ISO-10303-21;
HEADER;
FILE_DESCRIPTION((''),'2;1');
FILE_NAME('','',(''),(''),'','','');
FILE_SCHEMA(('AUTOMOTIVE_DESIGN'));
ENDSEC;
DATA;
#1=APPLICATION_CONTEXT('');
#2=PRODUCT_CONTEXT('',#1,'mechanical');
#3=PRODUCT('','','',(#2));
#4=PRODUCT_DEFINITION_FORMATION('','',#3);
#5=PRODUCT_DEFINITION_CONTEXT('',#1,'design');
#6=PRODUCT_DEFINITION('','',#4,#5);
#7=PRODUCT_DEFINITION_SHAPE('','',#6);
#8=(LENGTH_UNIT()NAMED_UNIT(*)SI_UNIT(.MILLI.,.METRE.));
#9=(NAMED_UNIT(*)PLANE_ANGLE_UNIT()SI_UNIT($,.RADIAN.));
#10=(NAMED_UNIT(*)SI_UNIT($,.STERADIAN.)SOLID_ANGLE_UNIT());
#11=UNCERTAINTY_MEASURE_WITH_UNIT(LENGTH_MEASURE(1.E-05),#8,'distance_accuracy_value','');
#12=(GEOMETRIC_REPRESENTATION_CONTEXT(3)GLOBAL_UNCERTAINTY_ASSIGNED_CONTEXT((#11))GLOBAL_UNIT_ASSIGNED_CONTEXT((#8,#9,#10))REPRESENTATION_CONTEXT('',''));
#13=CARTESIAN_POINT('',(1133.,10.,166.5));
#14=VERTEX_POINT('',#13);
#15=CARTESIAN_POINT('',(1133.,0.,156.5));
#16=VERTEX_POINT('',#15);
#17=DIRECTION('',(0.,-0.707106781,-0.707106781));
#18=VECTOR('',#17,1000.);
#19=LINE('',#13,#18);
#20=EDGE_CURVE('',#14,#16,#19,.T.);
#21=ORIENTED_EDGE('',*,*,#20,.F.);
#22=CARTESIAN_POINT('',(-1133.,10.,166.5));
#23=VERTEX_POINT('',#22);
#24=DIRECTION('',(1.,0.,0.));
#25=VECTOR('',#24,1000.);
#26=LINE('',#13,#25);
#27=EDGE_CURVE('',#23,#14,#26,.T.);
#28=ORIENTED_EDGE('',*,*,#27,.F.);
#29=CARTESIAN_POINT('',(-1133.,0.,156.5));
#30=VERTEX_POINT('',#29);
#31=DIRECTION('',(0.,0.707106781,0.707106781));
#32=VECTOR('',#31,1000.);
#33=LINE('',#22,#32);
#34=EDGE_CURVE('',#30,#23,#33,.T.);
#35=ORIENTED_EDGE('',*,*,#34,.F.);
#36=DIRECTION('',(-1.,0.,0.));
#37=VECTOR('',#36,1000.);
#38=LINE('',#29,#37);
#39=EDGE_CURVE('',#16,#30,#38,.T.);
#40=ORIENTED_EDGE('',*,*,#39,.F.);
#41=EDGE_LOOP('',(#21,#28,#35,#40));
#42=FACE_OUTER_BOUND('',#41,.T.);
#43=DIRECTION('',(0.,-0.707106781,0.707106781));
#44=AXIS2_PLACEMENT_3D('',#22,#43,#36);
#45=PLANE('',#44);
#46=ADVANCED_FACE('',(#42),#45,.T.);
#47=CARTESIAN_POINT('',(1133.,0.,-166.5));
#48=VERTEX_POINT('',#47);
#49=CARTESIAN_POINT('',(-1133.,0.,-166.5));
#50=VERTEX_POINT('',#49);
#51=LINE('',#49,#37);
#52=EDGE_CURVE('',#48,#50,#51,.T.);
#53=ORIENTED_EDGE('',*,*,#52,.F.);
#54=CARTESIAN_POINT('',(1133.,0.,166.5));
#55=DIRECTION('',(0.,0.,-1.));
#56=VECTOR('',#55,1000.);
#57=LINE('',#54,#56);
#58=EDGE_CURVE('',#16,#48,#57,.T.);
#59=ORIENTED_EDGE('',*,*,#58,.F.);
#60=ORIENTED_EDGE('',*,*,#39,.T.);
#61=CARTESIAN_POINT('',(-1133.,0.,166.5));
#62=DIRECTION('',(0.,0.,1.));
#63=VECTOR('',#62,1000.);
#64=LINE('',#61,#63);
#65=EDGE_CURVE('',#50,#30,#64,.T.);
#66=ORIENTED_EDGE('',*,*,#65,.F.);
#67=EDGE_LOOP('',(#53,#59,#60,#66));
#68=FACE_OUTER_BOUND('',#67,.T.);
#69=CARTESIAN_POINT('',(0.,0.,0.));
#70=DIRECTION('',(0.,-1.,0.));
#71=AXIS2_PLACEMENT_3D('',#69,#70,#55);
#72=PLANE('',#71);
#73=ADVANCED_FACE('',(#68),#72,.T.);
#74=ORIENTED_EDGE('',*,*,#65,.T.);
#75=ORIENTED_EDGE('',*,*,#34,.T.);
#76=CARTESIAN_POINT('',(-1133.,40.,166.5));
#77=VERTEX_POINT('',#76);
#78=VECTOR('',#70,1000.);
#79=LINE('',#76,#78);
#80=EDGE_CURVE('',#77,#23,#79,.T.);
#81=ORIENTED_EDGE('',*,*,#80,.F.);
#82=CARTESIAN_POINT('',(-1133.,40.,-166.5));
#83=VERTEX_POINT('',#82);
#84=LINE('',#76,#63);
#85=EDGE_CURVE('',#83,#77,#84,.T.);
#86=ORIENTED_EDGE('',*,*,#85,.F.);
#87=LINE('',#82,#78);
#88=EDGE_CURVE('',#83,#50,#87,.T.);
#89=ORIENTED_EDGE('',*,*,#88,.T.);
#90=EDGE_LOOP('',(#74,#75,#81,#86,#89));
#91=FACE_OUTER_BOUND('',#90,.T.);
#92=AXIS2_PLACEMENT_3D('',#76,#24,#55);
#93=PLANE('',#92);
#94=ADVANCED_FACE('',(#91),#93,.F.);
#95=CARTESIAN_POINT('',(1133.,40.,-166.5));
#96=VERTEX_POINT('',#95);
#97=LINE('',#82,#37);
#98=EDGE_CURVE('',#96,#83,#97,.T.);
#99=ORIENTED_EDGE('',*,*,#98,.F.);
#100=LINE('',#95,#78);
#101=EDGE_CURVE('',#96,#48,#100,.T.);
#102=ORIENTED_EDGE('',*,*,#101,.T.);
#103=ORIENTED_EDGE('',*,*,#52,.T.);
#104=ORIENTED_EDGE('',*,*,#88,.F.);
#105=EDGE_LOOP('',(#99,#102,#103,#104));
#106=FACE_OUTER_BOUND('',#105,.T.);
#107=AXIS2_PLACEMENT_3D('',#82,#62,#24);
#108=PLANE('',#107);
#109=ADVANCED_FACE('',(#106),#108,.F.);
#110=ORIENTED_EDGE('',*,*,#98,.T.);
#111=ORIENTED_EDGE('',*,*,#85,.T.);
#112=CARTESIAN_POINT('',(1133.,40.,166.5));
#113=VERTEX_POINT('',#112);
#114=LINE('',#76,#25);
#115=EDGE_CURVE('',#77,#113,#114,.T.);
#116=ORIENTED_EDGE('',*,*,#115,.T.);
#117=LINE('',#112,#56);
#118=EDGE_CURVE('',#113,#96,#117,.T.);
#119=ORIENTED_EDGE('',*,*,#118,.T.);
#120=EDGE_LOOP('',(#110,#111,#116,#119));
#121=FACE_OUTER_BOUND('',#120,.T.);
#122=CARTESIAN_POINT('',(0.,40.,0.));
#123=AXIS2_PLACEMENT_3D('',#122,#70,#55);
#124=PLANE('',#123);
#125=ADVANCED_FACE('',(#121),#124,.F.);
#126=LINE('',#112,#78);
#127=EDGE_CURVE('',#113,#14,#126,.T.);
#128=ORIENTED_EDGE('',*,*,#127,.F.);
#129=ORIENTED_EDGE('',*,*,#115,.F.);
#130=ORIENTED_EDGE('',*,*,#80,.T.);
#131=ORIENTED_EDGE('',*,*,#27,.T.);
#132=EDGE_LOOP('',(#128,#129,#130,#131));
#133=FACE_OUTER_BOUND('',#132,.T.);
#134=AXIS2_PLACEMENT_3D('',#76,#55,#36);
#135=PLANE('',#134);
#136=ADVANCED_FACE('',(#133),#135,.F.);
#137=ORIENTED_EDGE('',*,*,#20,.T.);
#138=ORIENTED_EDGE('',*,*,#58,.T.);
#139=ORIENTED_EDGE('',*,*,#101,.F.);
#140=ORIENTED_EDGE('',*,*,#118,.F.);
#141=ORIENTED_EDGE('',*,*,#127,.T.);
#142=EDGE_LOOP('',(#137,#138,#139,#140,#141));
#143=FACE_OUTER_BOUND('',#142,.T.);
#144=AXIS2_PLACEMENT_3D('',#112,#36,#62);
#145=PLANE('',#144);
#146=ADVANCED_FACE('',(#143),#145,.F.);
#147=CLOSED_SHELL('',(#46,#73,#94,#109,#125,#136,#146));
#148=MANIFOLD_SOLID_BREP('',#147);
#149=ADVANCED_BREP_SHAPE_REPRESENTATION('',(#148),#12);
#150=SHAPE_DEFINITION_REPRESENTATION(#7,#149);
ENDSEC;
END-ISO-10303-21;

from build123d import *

# Parameters (mm, degrees)
SKETCH_1_W      = 2266
SKETCH_1_H      = 333
EXTRUDE_1_DEPTH = 40
CHAMFER_1_SIZE  = 10


with BuildPart() as part:
    # 草图1 → 凸台-拉伸1 (new body)
    with BuildSketch(Plane(origin=(0, 0, 0), x_dir=(1, 0, 0), z_dir=(0, 1, 0))):
        Rectangle(SKETCH_1_W, SKETCH_1_H)
    extrude(amount=EXTRUDE_1_DEPTH)

    # 倒角1
    chamfer_1_edges = [part.edges().sort_by_distance(p)[0] for p in [
        (0, 0, 166.5),
    ]]
    chamfer(chamfer_1_edges, length=CHAMFER_1_SIZE)


solid = part.part
